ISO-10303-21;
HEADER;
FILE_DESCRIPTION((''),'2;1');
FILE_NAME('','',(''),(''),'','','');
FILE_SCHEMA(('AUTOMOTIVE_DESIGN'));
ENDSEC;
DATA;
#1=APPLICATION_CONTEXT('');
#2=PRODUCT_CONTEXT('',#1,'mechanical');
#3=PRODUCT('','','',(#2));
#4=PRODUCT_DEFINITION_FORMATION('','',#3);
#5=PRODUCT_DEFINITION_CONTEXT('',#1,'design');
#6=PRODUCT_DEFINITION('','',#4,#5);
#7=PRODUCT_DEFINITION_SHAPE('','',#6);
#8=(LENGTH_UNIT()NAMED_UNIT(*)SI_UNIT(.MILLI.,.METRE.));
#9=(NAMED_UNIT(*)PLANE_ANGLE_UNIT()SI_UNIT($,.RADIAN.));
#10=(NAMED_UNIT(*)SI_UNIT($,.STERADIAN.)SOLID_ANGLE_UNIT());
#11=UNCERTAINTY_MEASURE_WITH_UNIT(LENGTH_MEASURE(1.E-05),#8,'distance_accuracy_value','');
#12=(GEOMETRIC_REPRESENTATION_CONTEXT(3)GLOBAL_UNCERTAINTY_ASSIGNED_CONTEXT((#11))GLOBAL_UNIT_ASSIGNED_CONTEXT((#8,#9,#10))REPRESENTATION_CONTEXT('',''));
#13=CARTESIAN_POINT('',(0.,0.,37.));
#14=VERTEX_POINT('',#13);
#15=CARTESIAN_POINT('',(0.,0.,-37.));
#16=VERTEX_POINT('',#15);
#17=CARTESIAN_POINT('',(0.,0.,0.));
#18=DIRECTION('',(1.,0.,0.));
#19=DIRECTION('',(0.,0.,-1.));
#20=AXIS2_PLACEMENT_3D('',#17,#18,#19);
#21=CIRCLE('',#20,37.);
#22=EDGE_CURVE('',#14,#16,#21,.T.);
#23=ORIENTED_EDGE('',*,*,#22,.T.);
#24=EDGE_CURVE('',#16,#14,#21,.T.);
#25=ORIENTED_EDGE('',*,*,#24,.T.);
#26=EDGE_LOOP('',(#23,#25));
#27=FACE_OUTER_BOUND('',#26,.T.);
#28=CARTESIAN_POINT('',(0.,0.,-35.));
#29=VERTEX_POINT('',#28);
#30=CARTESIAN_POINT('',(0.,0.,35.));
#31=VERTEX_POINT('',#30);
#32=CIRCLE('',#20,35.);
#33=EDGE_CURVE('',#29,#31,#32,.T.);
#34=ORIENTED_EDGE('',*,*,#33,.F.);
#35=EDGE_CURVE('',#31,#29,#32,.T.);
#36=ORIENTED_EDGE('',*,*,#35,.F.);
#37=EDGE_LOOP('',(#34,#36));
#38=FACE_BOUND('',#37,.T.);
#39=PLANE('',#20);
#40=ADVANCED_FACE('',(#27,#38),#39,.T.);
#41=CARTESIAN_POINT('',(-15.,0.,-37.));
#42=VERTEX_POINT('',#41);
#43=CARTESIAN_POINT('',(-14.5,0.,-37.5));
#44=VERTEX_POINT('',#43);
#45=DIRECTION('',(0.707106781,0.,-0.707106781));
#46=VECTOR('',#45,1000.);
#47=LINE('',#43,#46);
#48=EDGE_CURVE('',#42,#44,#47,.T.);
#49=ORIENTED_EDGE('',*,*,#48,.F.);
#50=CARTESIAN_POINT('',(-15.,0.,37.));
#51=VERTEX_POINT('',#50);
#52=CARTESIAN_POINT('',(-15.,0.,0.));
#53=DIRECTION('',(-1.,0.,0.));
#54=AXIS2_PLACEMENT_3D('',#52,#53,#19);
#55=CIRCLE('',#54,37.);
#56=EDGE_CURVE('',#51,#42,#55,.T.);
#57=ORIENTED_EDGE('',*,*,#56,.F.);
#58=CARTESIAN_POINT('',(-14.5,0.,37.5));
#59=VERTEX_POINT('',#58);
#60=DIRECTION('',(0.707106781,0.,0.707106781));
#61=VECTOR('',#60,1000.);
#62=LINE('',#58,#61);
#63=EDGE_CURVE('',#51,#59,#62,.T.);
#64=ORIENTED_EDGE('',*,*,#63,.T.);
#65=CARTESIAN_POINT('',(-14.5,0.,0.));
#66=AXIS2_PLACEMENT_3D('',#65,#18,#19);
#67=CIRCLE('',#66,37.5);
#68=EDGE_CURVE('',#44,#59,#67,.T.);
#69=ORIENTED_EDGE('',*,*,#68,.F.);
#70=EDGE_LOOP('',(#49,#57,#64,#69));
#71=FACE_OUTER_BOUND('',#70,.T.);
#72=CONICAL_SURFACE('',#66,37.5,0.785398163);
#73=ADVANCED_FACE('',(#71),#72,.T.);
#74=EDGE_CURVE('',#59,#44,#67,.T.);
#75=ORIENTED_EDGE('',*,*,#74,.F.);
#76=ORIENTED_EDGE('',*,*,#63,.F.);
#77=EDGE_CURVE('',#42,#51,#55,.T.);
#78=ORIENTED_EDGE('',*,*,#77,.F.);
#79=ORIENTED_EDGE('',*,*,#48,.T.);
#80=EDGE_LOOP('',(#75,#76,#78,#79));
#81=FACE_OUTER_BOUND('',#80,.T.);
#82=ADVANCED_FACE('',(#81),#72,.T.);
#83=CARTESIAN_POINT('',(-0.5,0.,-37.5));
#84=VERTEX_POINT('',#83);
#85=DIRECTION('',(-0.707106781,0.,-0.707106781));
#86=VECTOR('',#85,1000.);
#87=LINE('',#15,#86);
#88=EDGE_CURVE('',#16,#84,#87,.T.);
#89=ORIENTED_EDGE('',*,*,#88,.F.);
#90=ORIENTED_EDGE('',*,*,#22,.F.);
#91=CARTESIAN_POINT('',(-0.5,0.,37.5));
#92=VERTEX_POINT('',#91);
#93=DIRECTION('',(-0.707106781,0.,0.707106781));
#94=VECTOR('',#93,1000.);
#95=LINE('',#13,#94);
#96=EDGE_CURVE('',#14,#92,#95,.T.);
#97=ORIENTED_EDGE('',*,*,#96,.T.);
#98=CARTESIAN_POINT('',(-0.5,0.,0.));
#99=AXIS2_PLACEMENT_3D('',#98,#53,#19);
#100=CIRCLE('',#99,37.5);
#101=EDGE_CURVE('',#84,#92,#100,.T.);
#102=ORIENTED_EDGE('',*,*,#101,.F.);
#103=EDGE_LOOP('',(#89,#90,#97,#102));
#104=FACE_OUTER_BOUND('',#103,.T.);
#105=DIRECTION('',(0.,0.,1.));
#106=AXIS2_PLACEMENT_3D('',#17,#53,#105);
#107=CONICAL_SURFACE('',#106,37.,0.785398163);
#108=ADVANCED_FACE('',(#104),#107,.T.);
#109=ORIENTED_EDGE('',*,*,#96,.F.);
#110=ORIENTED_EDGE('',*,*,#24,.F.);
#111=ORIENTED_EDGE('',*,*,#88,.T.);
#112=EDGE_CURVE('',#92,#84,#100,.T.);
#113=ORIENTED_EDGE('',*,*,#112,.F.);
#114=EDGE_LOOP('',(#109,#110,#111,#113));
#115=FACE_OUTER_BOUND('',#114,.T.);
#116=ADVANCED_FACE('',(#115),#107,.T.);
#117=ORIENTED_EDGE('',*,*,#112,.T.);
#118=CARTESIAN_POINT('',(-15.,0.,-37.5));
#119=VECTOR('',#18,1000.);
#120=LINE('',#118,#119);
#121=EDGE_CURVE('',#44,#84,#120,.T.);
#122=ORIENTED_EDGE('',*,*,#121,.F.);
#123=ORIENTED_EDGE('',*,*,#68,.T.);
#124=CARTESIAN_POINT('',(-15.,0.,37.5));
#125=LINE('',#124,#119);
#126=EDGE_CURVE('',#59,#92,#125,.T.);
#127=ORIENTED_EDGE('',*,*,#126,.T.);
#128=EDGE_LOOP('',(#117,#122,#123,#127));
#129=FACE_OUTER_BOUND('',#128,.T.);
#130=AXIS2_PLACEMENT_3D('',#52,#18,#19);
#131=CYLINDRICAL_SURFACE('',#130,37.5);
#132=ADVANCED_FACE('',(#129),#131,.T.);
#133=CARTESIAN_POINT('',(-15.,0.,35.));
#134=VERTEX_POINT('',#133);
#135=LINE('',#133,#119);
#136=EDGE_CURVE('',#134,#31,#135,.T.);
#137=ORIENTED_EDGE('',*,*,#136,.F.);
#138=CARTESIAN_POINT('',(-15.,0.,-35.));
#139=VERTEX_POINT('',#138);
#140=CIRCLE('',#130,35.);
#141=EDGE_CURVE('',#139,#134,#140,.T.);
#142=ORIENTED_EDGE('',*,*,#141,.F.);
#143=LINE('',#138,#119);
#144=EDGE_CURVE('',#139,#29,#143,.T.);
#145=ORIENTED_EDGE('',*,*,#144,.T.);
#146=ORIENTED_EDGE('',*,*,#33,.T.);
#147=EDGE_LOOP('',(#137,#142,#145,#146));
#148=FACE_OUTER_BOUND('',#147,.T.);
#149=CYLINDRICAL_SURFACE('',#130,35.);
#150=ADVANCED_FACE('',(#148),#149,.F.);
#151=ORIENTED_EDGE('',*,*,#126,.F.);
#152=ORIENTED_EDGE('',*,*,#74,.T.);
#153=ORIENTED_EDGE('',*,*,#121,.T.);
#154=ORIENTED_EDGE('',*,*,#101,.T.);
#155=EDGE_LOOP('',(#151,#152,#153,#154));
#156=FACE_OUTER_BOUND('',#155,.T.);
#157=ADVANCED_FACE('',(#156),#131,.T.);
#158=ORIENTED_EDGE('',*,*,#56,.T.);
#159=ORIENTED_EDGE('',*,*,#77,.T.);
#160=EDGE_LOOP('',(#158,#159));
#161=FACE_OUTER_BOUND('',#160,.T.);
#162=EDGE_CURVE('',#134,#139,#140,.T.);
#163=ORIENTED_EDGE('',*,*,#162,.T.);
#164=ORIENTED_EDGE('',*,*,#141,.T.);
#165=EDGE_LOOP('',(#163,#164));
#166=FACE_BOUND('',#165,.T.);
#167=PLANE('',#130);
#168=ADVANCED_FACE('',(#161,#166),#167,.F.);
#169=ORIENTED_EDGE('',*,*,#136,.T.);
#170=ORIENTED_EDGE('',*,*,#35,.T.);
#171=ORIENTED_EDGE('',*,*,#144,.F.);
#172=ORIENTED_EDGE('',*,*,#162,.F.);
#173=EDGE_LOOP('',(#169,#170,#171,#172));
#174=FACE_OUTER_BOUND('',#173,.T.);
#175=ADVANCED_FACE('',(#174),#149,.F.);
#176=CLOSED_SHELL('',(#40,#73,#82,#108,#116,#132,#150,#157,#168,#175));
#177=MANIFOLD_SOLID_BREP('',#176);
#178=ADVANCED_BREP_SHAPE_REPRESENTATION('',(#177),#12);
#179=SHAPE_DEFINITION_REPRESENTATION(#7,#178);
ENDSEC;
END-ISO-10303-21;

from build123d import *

# Parameters (mm, degrees)
SKETCH2_R           = 37.5
SKETCH2_R_2         = 35
BOSS_EXTRUDE1_DEPTH = 15
CHAMFER1_SIZE       = 0.5


with BuildPart() as part:
    # Sketch2 → Boss-Extrude1 (new body)
    with BuildSketch(Plane(origin=(0, 0, 0), x_dir=(0, 0, -1), z_dir=(1, 0, 0))):
        Circle(SKETCH2_R)
        Circle(SKETCH2_R_2, mode=Mode.SUBTRACT)
    extrude(amount=-BOSS_EXTRUDE1_DEPTH)

    # Chamfer1
    chamfer1_edges = [part.edges().sort_by_distance(p)[0] for p in [
        (0, 0, 37.5),
        (-15, 0, 37.5),
    ]]
    chamfer(chamfer1_edges, length=CHAMFER1_SIZE)


solid = part.part
